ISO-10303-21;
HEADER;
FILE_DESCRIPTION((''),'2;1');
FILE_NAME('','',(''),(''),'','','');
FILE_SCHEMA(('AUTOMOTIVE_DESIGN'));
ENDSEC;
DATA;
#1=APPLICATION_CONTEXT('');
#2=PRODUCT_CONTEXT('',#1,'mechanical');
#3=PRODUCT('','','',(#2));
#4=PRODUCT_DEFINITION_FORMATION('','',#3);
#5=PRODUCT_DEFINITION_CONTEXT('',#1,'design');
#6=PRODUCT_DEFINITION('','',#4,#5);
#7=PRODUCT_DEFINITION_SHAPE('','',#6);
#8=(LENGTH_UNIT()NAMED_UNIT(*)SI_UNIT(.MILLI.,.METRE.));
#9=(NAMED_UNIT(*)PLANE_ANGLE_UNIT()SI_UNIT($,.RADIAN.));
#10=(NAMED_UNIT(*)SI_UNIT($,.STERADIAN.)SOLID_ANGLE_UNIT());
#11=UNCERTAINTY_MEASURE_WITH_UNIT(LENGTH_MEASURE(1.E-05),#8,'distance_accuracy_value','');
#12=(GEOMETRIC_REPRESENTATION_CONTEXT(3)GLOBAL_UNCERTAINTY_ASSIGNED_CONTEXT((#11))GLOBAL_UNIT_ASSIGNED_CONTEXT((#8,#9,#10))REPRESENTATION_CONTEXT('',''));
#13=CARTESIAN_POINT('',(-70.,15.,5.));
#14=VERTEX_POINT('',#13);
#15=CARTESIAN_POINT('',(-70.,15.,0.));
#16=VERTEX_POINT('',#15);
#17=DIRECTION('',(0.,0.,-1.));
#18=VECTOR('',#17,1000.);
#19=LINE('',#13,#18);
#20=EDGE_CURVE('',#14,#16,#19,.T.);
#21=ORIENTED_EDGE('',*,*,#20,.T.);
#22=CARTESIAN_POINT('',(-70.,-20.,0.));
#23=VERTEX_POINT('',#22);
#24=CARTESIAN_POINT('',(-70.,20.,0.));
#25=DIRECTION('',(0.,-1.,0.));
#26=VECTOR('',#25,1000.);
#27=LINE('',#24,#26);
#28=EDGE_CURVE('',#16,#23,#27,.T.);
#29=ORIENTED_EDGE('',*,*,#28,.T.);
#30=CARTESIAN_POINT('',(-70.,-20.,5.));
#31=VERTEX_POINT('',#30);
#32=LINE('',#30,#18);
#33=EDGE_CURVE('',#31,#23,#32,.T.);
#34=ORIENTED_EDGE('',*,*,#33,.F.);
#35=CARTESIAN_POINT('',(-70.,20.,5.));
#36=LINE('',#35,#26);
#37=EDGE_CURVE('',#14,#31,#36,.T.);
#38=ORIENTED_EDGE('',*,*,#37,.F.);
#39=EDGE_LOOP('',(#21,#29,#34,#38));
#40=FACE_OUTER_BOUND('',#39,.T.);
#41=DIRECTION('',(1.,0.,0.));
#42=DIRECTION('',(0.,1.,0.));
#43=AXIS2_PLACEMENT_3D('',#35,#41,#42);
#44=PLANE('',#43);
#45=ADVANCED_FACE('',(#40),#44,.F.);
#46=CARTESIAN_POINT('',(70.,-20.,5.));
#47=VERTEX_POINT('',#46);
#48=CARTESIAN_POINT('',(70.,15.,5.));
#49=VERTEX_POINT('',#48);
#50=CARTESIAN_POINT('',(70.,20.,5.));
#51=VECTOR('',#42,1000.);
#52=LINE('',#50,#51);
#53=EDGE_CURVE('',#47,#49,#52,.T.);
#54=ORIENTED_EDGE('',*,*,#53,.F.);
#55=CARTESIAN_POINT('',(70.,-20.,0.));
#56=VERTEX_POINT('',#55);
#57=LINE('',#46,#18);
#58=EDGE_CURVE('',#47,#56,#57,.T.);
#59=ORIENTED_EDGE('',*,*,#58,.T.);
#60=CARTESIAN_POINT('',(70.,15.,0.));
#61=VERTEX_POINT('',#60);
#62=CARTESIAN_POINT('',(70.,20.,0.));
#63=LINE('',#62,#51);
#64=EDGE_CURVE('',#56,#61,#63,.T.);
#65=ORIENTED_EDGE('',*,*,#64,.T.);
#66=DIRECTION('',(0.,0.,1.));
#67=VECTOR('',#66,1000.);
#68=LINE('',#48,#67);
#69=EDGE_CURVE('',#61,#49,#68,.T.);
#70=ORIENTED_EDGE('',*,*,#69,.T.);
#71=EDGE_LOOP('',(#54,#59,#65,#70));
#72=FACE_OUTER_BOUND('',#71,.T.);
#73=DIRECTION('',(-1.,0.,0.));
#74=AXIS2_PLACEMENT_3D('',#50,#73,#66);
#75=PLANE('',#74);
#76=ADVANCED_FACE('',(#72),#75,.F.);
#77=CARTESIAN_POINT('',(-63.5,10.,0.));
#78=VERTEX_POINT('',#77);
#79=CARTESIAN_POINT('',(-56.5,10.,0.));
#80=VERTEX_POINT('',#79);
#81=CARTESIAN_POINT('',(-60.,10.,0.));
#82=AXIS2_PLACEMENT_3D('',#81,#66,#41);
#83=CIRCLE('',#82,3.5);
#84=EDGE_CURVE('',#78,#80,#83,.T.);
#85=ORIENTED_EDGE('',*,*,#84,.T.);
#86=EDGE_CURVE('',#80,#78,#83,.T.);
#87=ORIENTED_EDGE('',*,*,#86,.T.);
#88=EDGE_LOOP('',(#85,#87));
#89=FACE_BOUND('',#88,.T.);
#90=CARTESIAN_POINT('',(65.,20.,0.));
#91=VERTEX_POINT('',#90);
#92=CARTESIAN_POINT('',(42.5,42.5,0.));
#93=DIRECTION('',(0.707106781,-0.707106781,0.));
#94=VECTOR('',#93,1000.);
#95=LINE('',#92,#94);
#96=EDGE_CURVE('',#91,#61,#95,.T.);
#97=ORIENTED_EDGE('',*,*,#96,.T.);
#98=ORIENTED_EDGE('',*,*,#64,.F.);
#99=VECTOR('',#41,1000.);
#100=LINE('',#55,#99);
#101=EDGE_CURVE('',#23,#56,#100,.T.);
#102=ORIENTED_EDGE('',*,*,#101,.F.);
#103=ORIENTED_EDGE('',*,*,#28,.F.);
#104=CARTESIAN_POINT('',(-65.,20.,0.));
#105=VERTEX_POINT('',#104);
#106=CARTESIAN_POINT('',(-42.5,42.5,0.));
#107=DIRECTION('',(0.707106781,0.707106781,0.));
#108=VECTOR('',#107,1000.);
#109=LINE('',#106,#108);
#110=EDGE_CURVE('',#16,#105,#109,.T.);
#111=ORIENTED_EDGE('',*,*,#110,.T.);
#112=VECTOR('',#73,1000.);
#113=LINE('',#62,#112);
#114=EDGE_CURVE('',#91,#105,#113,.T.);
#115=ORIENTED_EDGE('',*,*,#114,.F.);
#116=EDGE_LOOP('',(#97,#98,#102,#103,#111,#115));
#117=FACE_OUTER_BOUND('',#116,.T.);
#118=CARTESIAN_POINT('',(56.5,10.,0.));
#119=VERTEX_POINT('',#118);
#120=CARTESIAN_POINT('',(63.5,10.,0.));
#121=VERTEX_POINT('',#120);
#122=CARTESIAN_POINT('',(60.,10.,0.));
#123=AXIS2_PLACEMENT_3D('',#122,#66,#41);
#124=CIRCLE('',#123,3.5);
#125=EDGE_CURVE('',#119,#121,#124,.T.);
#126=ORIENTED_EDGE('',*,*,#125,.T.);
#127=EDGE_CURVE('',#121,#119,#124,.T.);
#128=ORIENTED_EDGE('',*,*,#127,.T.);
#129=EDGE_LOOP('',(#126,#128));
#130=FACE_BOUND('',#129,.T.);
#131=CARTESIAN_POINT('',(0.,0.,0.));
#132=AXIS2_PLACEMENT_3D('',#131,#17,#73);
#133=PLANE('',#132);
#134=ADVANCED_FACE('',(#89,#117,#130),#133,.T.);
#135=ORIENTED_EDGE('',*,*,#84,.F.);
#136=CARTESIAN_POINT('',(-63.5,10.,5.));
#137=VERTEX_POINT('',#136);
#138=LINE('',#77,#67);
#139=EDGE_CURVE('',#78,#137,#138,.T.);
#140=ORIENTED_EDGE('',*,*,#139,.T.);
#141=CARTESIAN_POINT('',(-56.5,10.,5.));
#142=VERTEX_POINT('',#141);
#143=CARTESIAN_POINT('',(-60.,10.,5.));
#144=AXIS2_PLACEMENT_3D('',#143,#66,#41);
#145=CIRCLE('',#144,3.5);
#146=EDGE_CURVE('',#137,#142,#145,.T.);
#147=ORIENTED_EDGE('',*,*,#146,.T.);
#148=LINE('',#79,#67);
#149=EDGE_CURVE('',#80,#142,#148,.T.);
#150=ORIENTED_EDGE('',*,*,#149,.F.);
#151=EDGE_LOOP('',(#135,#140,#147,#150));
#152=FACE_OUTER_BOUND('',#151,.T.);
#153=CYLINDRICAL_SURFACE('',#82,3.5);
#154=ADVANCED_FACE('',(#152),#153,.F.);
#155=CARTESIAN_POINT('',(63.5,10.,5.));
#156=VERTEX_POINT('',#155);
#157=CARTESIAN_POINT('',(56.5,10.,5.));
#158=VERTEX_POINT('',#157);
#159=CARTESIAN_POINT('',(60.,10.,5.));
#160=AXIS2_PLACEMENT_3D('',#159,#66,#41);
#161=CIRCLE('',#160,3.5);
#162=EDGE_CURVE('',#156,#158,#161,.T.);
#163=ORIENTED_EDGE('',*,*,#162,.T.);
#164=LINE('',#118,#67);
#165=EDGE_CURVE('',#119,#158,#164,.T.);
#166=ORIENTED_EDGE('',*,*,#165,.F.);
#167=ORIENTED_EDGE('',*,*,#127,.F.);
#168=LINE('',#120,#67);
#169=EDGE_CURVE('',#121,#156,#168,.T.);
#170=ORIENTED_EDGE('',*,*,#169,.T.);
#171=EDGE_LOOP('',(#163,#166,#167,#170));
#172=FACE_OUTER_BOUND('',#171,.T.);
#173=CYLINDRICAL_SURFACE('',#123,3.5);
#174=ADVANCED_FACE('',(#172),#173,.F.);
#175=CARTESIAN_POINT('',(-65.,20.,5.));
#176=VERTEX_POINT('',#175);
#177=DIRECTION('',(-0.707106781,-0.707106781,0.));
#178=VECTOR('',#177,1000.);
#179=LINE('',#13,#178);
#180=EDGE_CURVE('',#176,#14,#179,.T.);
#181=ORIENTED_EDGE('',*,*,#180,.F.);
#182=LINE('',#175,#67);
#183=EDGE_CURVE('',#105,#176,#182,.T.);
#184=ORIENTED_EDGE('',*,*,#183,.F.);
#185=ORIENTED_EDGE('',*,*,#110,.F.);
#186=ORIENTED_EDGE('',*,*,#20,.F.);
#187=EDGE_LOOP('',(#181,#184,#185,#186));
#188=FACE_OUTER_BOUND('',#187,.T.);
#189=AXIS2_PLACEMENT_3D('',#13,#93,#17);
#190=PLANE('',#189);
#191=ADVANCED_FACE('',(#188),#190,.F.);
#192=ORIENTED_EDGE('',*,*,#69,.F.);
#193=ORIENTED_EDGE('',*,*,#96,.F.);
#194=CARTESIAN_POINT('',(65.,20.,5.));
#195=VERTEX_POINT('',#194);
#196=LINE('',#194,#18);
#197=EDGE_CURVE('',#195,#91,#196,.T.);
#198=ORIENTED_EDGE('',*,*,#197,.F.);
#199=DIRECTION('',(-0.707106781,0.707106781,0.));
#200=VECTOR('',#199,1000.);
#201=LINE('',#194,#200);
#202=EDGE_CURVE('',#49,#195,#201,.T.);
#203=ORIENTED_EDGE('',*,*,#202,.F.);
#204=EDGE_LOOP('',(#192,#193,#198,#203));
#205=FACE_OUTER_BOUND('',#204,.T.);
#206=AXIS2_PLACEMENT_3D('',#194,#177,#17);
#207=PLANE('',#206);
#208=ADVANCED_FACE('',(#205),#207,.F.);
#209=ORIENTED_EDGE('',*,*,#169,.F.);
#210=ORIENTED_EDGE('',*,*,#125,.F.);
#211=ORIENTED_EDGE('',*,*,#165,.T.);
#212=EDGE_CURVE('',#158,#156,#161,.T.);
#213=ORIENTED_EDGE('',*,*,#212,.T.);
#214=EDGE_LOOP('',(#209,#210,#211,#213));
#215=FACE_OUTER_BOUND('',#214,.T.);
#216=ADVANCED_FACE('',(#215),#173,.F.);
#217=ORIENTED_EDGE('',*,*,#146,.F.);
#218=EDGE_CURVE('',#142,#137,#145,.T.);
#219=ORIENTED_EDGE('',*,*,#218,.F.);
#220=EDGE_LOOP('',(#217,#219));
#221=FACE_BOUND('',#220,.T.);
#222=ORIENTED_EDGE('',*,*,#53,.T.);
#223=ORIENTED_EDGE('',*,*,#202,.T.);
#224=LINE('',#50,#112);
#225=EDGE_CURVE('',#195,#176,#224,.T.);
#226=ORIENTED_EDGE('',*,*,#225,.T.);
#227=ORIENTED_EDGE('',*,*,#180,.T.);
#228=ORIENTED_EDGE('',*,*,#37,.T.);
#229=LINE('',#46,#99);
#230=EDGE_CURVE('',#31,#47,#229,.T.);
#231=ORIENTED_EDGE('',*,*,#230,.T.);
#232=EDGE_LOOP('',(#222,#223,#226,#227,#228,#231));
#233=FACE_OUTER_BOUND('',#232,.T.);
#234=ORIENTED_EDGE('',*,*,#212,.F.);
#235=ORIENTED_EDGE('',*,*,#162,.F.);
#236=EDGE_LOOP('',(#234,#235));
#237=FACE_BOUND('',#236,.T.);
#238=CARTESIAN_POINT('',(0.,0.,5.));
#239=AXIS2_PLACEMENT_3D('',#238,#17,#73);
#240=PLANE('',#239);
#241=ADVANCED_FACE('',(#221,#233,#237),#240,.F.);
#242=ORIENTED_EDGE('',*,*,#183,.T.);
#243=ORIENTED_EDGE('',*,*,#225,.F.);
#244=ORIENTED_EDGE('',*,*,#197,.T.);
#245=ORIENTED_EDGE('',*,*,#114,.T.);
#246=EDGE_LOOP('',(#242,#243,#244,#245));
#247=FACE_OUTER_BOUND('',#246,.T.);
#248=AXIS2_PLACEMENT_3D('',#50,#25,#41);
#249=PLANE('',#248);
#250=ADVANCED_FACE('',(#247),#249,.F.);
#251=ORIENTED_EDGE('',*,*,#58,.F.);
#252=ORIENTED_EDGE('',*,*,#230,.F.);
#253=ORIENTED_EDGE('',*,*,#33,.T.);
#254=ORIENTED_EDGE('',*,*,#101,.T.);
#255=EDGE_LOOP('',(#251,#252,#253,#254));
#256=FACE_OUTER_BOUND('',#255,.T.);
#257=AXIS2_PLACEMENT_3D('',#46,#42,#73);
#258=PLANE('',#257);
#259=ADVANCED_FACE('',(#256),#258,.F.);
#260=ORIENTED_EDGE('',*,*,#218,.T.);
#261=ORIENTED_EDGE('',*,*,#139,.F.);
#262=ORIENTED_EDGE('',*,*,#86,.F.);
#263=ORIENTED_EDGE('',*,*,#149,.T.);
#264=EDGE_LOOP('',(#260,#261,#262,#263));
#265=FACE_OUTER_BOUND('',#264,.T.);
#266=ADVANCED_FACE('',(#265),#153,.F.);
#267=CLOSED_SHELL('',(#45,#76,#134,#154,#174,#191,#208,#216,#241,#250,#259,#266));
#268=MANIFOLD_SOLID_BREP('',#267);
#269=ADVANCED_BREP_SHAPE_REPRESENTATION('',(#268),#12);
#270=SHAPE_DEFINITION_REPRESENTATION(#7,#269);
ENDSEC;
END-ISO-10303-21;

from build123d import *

# Parameters (mm, degrees)
SKETCH_1_W          = 140
SKETCH_1_H          = 40
EXTRUDE_1_DEPTH     = 5
SKETCH_2_R          = 3.5
CUT_EXTRUDE_1_DEPTH = 5
CHAMFER_1_SIZE      = 5


with BuildPart() as part:
    # 草图1 → 凸台-拉伸1 (new body)
    with BuildSketch(Plane.XY):
        Rectangle(SKETCH_1_W, SKETCH_1_H)
    extrude(amount=EXTRUDE_1_DEPTH)

    # 草图2 → 切除-拉伸1 (cut)
    with BuildSketch(Plane.XY.offset(5)):
        with Locations((-60, 10)):
            Circle(SKETCH_2_R)
        with Locations((60, 10)):
            Circle(SKETCH_2_R)
    extrude(amount=-CUT_EXTRUDE_1_DEPTH, mode=Mode.SUBTRACT)

    # 倒角1
    chamfer_1_edges = [part.edges().sort_by_distance(p)[0] for p in [
        (-70, 20, 2.5),
        (70, 20, 2.5),
    ]]
    chamfer(chamfer_1_edges, length=CHAMFER_1_SIZE)


solid = part.part
